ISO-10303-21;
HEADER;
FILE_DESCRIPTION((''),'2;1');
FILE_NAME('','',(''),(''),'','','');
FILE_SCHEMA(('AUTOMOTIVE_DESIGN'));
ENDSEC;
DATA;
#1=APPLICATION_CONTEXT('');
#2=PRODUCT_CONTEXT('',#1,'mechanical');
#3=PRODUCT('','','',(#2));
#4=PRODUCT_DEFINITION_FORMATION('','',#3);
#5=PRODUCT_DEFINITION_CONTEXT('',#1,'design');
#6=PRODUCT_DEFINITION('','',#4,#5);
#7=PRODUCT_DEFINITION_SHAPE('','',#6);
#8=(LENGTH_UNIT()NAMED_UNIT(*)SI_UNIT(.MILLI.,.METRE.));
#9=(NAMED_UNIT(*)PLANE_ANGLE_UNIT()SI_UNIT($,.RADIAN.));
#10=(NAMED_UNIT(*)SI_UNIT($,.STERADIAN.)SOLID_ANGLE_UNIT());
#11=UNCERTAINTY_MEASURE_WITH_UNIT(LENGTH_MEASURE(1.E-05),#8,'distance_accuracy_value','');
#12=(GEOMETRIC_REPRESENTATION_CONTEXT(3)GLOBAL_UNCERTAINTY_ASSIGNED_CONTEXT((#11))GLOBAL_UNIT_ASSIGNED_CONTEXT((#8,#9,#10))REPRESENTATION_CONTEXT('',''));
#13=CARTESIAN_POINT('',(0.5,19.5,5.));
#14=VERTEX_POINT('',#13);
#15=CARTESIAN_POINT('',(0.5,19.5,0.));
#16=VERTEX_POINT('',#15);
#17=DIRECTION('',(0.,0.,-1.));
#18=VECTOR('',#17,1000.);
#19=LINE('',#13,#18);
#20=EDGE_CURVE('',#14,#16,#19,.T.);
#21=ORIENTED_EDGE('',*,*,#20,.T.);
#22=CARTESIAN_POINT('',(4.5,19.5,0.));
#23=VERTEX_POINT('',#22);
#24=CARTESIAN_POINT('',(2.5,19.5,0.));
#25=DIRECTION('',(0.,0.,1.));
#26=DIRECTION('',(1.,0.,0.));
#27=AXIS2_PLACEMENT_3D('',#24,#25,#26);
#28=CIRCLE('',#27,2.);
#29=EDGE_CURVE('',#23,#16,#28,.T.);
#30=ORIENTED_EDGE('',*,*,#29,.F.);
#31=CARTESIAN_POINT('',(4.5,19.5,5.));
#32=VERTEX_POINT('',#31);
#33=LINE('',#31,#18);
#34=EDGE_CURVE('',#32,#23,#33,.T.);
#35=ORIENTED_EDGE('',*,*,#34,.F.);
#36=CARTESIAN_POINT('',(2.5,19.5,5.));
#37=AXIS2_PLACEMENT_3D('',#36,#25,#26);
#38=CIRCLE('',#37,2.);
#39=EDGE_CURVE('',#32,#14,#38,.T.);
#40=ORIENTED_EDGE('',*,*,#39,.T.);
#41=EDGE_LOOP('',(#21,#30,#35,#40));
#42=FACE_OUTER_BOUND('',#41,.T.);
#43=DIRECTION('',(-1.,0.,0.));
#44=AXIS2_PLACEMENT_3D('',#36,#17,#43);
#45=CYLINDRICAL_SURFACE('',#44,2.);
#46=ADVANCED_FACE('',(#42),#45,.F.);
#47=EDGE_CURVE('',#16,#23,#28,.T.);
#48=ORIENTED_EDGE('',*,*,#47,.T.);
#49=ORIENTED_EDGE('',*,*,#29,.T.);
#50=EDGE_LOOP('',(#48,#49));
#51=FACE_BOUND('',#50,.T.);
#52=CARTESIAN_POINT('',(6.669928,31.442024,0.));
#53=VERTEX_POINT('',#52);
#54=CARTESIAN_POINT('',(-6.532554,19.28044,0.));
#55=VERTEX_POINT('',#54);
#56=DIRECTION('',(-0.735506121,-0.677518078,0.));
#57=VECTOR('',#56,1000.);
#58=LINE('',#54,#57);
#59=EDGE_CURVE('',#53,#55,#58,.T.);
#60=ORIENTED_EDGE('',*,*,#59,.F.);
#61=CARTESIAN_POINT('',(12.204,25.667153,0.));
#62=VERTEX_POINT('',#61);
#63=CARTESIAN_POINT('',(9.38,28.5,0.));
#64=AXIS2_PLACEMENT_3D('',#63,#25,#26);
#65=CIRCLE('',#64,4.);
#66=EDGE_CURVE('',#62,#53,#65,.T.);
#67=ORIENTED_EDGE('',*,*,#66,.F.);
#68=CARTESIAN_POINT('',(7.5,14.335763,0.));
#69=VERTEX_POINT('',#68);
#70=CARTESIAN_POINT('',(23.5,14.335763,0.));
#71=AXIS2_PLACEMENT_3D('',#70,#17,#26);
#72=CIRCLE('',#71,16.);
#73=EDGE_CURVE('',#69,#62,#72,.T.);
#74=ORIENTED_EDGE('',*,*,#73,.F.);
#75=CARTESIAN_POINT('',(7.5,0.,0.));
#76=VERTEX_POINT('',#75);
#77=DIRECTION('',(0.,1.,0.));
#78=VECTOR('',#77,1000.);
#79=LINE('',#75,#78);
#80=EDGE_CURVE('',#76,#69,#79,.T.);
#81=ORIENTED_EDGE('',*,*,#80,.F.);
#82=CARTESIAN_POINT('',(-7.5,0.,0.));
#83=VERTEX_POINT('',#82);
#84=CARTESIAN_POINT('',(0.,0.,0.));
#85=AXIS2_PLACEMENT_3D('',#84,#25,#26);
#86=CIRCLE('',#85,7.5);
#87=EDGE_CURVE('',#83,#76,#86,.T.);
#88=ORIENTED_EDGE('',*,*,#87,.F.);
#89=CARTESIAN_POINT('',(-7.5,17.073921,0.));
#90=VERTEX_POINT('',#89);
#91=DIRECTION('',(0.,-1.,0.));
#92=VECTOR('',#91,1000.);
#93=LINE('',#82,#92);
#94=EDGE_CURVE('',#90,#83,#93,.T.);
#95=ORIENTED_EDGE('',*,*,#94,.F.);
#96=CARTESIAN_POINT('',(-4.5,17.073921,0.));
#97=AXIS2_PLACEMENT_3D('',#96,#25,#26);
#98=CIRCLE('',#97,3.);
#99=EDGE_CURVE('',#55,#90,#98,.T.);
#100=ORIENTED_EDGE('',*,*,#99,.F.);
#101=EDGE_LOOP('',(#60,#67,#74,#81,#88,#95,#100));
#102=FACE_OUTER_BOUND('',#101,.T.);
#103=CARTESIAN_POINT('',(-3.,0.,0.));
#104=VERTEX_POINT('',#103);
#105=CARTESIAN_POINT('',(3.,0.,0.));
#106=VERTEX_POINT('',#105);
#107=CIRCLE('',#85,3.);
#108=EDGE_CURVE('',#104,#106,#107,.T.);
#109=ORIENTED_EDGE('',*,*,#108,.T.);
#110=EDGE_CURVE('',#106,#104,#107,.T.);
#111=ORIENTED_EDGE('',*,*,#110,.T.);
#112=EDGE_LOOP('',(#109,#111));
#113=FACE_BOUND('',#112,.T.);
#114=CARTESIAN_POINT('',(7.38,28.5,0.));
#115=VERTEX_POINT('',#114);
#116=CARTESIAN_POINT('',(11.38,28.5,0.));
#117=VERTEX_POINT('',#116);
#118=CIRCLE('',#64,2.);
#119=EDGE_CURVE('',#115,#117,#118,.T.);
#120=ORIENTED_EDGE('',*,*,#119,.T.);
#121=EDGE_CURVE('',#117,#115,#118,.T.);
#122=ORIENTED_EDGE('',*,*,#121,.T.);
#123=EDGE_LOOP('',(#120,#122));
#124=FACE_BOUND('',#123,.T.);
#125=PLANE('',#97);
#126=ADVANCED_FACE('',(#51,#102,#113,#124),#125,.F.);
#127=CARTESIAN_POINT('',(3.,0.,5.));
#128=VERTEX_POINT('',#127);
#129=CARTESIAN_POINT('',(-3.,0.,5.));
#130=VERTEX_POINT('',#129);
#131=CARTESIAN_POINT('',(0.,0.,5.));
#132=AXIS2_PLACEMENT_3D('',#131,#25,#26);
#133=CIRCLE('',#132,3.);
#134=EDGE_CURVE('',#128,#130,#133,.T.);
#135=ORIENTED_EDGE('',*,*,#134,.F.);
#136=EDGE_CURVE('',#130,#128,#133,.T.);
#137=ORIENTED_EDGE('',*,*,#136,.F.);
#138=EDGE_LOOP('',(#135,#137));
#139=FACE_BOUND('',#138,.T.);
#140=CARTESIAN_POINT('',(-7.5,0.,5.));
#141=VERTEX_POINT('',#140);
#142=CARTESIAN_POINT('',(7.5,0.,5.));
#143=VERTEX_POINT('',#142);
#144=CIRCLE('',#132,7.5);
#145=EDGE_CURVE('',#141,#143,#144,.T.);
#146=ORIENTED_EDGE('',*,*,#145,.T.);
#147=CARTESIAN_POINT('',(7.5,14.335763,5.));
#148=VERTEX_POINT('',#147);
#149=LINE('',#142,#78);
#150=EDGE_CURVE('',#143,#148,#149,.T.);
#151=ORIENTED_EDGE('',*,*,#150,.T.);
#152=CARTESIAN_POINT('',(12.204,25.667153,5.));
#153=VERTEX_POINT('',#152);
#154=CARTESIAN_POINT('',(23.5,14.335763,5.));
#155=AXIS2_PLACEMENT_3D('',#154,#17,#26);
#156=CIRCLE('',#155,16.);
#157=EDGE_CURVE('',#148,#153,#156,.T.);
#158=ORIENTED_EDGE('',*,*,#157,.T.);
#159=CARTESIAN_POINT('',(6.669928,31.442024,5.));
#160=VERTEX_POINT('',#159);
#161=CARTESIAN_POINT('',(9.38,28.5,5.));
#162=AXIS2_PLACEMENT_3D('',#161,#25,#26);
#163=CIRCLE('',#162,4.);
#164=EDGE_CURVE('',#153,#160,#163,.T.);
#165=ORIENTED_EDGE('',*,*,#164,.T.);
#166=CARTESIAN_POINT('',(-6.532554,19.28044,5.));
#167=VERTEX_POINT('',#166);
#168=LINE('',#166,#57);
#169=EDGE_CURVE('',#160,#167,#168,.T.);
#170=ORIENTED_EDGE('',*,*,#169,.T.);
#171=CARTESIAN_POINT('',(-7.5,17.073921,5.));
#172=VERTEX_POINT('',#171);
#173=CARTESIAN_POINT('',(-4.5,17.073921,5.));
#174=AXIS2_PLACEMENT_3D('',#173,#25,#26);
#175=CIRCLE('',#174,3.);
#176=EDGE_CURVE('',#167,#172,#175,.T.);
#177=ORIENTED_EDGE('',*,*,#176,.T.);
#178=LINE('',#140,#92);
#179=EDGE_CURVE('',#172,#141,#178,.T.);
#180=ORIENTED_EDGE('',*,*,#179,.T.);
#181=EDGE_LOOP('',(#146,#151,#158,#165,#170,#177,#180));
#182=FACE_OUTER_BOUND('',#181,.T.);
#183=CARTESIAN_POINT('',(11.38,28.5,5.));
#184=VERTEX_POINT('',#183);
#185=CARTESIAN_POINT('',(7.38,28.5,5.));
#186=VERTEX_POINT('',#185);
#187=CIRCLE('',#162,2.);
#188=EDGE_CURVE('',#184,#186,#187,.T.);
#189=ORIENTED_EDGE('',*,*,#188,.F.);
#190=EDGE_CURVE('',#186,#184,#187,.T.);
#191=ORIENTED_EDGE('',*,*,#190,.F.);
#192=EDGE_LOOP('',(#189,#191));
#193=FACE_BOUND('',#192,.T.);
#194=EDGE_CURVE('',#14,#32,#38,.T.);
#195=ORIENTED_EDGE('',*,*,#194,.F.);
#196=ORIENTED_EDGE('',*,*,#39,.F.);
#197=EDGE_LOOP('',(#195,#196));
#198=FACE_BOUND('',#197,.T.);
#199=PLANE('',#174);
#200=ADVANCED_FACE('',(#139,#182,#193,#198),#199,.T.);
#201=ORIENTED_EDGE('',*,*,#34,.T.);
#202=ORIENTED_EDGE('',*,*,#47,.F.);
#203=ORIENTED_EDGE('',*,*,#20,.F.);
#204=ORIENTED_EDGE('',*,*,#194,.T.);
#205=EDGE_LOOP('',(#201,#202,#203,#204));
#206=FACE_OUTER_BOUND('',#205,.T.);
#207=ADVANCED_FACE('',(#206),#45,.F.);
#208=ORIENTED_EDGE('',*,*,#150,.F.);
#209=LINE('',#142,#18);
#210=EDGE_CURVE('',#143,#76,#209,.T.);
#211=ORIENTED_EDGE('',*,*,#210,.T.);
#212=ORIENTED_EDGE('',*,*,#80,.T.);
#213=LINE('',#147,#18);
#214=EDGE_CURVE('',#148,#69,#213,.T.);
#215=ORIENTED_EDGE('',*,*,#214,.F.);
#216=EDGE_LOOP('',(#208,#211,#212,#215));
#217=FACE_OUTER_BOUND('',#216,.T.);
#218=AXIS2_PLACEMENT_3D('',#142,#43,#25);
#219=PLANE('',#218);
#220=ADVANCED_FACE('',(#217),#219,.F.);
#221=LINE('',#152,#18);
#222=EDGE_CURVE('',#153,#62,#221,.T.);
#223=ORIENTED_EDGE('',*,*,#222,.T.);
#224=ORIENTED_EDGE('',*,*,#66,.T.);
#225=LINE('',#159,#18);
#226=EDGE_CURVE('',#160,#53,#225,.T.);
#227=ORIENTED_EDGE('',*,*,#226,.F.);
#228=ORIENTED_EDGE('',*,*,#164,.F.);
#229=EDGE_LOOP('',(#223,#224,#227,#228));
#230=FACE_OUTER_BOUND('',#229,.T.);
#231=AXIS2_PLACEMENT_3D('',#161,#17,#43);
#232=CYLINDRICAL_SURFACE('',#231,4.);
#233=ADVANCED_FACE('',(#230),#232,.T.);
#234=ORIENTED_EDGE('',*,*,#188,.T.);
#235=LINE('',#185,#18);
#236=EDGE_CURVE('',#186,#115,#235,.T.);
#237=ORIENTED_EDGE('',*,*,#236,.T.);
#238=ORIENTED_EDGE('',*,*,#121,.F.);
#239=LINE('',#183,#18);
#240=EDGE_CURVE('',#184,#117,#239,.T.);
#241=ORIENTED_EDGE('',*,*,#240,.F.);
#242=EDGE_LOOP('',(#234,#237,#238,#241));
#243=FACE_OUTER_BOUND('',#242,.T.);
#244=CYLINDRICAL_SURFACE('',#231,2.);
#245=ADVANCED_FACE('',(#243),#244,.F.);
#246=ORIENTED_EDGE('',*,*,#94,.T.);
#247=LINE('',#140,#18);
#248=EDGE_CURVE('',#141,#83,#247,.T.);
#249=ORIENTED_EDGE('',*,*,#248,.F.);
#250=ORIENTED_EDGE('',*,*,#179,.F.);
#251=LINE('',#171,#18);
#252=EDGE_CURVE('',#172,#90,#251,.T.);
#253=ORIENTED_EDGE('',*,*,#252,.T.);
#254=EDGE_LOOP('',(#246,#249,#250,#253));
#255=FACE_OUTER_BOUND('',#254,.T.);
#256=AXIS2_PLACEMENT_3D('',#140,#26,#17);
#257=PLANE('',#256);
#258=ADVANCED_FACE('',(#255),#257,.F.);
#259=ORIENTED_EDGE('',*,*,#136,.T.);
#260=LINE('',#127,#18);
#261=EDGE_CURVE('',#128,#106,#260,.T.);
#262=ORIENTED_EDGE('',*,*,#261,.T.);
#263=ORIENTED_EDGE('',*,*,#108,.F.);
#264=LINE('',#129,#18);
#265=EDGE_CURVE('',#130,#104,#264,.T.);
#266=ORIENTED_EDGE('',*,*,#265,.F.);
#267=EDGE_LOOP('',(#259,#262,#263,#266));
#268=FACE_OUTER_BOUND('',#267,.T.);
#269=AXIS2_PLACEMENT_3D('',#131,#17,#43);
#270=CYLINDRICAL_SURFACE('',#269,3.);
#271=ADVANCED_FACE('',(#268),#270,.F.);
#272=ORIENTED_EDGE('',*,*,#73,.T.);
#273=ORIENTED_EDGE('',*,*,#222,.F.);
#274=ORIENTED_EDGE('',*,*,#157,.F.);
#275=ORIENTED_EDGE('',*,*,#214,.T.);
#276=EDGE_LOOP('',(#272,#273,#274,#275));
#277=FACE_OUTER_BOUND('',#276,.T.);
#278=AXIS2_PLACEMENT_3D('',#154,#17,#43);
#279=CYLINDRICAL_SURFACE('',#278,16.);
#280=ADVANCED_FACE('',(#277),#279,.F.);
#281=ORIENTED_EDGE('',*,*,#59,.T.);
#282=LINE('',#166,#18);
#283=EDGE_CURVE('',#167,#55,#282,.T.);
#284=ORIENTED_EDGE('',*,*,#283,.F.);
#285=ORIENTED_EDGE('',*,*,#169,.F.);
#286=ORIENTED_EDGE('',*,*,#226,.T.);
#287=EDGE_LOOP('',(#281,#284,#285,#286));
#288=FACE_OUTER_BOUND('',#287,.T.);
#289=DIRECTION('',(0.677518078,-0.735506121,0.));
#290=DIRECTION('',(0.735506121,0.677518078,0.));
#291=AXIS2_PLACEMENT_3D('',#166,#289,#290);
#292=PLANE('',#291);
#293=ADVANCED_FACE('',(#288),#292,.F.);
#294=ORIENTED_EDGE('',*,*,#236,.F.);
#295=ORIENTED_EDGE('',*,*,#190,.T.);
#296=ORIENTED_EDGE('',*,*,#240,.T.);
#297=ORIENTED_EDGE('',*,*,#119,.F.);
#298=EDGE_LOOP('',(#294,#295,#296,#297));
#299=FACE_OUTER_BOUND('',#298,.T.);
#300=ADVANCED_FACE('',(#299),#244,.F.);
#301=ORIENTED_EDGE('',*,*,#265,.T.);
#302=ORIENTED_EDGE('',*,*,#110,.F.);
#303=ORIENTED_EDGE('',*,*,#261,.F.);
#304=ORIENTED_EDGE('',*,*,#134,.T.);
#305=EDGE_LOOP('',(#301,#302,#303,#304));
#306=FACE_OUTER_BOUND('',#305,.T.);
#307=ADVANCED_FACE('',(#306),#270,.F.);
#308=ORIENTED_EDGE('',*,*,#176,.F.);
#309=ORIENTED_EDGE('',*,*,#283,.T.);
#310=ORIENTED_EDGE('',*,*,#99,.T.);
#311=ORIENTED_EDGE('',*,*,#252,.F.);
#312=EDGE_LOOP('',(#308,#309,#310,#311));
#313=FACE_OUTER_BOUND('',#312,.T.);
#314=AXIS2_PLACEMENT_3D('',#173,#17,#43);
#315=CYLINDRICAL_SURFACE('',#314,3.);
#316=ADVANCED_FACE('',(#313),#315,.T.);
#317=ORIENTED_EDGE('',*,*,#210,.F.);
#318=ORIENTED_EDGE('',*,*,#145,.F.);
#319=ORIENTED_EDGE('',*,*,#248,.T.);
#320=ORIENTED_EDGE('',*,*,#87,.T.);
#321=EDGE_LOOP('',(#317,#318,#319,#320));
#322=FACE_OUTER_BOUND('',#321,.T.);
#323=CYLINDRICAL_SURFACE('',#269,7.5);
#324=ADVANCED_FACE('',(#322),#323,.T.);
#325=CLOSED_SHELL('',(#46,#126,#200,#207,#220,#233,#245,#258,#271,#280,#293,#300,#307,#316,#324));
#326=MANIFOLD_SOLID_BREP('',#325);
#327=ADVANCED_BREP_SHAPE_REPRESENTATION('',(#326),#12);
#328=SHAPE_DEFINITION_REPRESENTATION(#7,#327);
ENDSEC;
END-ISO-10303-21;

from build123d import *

# Parameters (mm, degrees)
SKETCH1_R           = 3
SKETCH1_R_2         = 2
BOSS_EXTRUDE1_DEPTH = 5


with BuildPart() as part:
    # Sketch1 → Boss-Extrude1 (new body)
    with BuildSketch(Plane.XY):
        with BuildLine():
            Line((-7.5, 0), (-7.5, 17.073921172))
            ThreePointArc((-7.5, 17.073921172), (-7.247513667, 18.278565788), (-6.532554233, 19.280439536))
            Line((-6.532554233, 19.280439536), (6.669927689, 31.442024485))
            ThreePointArc((6.669927689, 31.442024485), (12.26799775, 31.26757457), (12.204, 25.667152669))
            ThreePointArc((12.204, 25.667152669), (8.722720142, 20.47025599), (7.5, 14.335763346))
            Line((7.5, 14.335763346), (7.5, 0))
            ThreePointArc((7.5, 0), (0, -7.5), (-7.5, 0))
        make_face()
        Circle(SKETCH1_R, mode=Mode.SUBTRACT)
        with Locations((2.5, 19.5)):
            Circle(SKETCH1_R_2, mode=Mode.SUBTRACT)
        with Locations((9.38, 28.5)):
            Circle(SKETCH1_R_2, mode=Mode.SUBTRACT)
    extrude(amount=BOSS_EXTRUDE1_DEPTH)


solid = part.part
